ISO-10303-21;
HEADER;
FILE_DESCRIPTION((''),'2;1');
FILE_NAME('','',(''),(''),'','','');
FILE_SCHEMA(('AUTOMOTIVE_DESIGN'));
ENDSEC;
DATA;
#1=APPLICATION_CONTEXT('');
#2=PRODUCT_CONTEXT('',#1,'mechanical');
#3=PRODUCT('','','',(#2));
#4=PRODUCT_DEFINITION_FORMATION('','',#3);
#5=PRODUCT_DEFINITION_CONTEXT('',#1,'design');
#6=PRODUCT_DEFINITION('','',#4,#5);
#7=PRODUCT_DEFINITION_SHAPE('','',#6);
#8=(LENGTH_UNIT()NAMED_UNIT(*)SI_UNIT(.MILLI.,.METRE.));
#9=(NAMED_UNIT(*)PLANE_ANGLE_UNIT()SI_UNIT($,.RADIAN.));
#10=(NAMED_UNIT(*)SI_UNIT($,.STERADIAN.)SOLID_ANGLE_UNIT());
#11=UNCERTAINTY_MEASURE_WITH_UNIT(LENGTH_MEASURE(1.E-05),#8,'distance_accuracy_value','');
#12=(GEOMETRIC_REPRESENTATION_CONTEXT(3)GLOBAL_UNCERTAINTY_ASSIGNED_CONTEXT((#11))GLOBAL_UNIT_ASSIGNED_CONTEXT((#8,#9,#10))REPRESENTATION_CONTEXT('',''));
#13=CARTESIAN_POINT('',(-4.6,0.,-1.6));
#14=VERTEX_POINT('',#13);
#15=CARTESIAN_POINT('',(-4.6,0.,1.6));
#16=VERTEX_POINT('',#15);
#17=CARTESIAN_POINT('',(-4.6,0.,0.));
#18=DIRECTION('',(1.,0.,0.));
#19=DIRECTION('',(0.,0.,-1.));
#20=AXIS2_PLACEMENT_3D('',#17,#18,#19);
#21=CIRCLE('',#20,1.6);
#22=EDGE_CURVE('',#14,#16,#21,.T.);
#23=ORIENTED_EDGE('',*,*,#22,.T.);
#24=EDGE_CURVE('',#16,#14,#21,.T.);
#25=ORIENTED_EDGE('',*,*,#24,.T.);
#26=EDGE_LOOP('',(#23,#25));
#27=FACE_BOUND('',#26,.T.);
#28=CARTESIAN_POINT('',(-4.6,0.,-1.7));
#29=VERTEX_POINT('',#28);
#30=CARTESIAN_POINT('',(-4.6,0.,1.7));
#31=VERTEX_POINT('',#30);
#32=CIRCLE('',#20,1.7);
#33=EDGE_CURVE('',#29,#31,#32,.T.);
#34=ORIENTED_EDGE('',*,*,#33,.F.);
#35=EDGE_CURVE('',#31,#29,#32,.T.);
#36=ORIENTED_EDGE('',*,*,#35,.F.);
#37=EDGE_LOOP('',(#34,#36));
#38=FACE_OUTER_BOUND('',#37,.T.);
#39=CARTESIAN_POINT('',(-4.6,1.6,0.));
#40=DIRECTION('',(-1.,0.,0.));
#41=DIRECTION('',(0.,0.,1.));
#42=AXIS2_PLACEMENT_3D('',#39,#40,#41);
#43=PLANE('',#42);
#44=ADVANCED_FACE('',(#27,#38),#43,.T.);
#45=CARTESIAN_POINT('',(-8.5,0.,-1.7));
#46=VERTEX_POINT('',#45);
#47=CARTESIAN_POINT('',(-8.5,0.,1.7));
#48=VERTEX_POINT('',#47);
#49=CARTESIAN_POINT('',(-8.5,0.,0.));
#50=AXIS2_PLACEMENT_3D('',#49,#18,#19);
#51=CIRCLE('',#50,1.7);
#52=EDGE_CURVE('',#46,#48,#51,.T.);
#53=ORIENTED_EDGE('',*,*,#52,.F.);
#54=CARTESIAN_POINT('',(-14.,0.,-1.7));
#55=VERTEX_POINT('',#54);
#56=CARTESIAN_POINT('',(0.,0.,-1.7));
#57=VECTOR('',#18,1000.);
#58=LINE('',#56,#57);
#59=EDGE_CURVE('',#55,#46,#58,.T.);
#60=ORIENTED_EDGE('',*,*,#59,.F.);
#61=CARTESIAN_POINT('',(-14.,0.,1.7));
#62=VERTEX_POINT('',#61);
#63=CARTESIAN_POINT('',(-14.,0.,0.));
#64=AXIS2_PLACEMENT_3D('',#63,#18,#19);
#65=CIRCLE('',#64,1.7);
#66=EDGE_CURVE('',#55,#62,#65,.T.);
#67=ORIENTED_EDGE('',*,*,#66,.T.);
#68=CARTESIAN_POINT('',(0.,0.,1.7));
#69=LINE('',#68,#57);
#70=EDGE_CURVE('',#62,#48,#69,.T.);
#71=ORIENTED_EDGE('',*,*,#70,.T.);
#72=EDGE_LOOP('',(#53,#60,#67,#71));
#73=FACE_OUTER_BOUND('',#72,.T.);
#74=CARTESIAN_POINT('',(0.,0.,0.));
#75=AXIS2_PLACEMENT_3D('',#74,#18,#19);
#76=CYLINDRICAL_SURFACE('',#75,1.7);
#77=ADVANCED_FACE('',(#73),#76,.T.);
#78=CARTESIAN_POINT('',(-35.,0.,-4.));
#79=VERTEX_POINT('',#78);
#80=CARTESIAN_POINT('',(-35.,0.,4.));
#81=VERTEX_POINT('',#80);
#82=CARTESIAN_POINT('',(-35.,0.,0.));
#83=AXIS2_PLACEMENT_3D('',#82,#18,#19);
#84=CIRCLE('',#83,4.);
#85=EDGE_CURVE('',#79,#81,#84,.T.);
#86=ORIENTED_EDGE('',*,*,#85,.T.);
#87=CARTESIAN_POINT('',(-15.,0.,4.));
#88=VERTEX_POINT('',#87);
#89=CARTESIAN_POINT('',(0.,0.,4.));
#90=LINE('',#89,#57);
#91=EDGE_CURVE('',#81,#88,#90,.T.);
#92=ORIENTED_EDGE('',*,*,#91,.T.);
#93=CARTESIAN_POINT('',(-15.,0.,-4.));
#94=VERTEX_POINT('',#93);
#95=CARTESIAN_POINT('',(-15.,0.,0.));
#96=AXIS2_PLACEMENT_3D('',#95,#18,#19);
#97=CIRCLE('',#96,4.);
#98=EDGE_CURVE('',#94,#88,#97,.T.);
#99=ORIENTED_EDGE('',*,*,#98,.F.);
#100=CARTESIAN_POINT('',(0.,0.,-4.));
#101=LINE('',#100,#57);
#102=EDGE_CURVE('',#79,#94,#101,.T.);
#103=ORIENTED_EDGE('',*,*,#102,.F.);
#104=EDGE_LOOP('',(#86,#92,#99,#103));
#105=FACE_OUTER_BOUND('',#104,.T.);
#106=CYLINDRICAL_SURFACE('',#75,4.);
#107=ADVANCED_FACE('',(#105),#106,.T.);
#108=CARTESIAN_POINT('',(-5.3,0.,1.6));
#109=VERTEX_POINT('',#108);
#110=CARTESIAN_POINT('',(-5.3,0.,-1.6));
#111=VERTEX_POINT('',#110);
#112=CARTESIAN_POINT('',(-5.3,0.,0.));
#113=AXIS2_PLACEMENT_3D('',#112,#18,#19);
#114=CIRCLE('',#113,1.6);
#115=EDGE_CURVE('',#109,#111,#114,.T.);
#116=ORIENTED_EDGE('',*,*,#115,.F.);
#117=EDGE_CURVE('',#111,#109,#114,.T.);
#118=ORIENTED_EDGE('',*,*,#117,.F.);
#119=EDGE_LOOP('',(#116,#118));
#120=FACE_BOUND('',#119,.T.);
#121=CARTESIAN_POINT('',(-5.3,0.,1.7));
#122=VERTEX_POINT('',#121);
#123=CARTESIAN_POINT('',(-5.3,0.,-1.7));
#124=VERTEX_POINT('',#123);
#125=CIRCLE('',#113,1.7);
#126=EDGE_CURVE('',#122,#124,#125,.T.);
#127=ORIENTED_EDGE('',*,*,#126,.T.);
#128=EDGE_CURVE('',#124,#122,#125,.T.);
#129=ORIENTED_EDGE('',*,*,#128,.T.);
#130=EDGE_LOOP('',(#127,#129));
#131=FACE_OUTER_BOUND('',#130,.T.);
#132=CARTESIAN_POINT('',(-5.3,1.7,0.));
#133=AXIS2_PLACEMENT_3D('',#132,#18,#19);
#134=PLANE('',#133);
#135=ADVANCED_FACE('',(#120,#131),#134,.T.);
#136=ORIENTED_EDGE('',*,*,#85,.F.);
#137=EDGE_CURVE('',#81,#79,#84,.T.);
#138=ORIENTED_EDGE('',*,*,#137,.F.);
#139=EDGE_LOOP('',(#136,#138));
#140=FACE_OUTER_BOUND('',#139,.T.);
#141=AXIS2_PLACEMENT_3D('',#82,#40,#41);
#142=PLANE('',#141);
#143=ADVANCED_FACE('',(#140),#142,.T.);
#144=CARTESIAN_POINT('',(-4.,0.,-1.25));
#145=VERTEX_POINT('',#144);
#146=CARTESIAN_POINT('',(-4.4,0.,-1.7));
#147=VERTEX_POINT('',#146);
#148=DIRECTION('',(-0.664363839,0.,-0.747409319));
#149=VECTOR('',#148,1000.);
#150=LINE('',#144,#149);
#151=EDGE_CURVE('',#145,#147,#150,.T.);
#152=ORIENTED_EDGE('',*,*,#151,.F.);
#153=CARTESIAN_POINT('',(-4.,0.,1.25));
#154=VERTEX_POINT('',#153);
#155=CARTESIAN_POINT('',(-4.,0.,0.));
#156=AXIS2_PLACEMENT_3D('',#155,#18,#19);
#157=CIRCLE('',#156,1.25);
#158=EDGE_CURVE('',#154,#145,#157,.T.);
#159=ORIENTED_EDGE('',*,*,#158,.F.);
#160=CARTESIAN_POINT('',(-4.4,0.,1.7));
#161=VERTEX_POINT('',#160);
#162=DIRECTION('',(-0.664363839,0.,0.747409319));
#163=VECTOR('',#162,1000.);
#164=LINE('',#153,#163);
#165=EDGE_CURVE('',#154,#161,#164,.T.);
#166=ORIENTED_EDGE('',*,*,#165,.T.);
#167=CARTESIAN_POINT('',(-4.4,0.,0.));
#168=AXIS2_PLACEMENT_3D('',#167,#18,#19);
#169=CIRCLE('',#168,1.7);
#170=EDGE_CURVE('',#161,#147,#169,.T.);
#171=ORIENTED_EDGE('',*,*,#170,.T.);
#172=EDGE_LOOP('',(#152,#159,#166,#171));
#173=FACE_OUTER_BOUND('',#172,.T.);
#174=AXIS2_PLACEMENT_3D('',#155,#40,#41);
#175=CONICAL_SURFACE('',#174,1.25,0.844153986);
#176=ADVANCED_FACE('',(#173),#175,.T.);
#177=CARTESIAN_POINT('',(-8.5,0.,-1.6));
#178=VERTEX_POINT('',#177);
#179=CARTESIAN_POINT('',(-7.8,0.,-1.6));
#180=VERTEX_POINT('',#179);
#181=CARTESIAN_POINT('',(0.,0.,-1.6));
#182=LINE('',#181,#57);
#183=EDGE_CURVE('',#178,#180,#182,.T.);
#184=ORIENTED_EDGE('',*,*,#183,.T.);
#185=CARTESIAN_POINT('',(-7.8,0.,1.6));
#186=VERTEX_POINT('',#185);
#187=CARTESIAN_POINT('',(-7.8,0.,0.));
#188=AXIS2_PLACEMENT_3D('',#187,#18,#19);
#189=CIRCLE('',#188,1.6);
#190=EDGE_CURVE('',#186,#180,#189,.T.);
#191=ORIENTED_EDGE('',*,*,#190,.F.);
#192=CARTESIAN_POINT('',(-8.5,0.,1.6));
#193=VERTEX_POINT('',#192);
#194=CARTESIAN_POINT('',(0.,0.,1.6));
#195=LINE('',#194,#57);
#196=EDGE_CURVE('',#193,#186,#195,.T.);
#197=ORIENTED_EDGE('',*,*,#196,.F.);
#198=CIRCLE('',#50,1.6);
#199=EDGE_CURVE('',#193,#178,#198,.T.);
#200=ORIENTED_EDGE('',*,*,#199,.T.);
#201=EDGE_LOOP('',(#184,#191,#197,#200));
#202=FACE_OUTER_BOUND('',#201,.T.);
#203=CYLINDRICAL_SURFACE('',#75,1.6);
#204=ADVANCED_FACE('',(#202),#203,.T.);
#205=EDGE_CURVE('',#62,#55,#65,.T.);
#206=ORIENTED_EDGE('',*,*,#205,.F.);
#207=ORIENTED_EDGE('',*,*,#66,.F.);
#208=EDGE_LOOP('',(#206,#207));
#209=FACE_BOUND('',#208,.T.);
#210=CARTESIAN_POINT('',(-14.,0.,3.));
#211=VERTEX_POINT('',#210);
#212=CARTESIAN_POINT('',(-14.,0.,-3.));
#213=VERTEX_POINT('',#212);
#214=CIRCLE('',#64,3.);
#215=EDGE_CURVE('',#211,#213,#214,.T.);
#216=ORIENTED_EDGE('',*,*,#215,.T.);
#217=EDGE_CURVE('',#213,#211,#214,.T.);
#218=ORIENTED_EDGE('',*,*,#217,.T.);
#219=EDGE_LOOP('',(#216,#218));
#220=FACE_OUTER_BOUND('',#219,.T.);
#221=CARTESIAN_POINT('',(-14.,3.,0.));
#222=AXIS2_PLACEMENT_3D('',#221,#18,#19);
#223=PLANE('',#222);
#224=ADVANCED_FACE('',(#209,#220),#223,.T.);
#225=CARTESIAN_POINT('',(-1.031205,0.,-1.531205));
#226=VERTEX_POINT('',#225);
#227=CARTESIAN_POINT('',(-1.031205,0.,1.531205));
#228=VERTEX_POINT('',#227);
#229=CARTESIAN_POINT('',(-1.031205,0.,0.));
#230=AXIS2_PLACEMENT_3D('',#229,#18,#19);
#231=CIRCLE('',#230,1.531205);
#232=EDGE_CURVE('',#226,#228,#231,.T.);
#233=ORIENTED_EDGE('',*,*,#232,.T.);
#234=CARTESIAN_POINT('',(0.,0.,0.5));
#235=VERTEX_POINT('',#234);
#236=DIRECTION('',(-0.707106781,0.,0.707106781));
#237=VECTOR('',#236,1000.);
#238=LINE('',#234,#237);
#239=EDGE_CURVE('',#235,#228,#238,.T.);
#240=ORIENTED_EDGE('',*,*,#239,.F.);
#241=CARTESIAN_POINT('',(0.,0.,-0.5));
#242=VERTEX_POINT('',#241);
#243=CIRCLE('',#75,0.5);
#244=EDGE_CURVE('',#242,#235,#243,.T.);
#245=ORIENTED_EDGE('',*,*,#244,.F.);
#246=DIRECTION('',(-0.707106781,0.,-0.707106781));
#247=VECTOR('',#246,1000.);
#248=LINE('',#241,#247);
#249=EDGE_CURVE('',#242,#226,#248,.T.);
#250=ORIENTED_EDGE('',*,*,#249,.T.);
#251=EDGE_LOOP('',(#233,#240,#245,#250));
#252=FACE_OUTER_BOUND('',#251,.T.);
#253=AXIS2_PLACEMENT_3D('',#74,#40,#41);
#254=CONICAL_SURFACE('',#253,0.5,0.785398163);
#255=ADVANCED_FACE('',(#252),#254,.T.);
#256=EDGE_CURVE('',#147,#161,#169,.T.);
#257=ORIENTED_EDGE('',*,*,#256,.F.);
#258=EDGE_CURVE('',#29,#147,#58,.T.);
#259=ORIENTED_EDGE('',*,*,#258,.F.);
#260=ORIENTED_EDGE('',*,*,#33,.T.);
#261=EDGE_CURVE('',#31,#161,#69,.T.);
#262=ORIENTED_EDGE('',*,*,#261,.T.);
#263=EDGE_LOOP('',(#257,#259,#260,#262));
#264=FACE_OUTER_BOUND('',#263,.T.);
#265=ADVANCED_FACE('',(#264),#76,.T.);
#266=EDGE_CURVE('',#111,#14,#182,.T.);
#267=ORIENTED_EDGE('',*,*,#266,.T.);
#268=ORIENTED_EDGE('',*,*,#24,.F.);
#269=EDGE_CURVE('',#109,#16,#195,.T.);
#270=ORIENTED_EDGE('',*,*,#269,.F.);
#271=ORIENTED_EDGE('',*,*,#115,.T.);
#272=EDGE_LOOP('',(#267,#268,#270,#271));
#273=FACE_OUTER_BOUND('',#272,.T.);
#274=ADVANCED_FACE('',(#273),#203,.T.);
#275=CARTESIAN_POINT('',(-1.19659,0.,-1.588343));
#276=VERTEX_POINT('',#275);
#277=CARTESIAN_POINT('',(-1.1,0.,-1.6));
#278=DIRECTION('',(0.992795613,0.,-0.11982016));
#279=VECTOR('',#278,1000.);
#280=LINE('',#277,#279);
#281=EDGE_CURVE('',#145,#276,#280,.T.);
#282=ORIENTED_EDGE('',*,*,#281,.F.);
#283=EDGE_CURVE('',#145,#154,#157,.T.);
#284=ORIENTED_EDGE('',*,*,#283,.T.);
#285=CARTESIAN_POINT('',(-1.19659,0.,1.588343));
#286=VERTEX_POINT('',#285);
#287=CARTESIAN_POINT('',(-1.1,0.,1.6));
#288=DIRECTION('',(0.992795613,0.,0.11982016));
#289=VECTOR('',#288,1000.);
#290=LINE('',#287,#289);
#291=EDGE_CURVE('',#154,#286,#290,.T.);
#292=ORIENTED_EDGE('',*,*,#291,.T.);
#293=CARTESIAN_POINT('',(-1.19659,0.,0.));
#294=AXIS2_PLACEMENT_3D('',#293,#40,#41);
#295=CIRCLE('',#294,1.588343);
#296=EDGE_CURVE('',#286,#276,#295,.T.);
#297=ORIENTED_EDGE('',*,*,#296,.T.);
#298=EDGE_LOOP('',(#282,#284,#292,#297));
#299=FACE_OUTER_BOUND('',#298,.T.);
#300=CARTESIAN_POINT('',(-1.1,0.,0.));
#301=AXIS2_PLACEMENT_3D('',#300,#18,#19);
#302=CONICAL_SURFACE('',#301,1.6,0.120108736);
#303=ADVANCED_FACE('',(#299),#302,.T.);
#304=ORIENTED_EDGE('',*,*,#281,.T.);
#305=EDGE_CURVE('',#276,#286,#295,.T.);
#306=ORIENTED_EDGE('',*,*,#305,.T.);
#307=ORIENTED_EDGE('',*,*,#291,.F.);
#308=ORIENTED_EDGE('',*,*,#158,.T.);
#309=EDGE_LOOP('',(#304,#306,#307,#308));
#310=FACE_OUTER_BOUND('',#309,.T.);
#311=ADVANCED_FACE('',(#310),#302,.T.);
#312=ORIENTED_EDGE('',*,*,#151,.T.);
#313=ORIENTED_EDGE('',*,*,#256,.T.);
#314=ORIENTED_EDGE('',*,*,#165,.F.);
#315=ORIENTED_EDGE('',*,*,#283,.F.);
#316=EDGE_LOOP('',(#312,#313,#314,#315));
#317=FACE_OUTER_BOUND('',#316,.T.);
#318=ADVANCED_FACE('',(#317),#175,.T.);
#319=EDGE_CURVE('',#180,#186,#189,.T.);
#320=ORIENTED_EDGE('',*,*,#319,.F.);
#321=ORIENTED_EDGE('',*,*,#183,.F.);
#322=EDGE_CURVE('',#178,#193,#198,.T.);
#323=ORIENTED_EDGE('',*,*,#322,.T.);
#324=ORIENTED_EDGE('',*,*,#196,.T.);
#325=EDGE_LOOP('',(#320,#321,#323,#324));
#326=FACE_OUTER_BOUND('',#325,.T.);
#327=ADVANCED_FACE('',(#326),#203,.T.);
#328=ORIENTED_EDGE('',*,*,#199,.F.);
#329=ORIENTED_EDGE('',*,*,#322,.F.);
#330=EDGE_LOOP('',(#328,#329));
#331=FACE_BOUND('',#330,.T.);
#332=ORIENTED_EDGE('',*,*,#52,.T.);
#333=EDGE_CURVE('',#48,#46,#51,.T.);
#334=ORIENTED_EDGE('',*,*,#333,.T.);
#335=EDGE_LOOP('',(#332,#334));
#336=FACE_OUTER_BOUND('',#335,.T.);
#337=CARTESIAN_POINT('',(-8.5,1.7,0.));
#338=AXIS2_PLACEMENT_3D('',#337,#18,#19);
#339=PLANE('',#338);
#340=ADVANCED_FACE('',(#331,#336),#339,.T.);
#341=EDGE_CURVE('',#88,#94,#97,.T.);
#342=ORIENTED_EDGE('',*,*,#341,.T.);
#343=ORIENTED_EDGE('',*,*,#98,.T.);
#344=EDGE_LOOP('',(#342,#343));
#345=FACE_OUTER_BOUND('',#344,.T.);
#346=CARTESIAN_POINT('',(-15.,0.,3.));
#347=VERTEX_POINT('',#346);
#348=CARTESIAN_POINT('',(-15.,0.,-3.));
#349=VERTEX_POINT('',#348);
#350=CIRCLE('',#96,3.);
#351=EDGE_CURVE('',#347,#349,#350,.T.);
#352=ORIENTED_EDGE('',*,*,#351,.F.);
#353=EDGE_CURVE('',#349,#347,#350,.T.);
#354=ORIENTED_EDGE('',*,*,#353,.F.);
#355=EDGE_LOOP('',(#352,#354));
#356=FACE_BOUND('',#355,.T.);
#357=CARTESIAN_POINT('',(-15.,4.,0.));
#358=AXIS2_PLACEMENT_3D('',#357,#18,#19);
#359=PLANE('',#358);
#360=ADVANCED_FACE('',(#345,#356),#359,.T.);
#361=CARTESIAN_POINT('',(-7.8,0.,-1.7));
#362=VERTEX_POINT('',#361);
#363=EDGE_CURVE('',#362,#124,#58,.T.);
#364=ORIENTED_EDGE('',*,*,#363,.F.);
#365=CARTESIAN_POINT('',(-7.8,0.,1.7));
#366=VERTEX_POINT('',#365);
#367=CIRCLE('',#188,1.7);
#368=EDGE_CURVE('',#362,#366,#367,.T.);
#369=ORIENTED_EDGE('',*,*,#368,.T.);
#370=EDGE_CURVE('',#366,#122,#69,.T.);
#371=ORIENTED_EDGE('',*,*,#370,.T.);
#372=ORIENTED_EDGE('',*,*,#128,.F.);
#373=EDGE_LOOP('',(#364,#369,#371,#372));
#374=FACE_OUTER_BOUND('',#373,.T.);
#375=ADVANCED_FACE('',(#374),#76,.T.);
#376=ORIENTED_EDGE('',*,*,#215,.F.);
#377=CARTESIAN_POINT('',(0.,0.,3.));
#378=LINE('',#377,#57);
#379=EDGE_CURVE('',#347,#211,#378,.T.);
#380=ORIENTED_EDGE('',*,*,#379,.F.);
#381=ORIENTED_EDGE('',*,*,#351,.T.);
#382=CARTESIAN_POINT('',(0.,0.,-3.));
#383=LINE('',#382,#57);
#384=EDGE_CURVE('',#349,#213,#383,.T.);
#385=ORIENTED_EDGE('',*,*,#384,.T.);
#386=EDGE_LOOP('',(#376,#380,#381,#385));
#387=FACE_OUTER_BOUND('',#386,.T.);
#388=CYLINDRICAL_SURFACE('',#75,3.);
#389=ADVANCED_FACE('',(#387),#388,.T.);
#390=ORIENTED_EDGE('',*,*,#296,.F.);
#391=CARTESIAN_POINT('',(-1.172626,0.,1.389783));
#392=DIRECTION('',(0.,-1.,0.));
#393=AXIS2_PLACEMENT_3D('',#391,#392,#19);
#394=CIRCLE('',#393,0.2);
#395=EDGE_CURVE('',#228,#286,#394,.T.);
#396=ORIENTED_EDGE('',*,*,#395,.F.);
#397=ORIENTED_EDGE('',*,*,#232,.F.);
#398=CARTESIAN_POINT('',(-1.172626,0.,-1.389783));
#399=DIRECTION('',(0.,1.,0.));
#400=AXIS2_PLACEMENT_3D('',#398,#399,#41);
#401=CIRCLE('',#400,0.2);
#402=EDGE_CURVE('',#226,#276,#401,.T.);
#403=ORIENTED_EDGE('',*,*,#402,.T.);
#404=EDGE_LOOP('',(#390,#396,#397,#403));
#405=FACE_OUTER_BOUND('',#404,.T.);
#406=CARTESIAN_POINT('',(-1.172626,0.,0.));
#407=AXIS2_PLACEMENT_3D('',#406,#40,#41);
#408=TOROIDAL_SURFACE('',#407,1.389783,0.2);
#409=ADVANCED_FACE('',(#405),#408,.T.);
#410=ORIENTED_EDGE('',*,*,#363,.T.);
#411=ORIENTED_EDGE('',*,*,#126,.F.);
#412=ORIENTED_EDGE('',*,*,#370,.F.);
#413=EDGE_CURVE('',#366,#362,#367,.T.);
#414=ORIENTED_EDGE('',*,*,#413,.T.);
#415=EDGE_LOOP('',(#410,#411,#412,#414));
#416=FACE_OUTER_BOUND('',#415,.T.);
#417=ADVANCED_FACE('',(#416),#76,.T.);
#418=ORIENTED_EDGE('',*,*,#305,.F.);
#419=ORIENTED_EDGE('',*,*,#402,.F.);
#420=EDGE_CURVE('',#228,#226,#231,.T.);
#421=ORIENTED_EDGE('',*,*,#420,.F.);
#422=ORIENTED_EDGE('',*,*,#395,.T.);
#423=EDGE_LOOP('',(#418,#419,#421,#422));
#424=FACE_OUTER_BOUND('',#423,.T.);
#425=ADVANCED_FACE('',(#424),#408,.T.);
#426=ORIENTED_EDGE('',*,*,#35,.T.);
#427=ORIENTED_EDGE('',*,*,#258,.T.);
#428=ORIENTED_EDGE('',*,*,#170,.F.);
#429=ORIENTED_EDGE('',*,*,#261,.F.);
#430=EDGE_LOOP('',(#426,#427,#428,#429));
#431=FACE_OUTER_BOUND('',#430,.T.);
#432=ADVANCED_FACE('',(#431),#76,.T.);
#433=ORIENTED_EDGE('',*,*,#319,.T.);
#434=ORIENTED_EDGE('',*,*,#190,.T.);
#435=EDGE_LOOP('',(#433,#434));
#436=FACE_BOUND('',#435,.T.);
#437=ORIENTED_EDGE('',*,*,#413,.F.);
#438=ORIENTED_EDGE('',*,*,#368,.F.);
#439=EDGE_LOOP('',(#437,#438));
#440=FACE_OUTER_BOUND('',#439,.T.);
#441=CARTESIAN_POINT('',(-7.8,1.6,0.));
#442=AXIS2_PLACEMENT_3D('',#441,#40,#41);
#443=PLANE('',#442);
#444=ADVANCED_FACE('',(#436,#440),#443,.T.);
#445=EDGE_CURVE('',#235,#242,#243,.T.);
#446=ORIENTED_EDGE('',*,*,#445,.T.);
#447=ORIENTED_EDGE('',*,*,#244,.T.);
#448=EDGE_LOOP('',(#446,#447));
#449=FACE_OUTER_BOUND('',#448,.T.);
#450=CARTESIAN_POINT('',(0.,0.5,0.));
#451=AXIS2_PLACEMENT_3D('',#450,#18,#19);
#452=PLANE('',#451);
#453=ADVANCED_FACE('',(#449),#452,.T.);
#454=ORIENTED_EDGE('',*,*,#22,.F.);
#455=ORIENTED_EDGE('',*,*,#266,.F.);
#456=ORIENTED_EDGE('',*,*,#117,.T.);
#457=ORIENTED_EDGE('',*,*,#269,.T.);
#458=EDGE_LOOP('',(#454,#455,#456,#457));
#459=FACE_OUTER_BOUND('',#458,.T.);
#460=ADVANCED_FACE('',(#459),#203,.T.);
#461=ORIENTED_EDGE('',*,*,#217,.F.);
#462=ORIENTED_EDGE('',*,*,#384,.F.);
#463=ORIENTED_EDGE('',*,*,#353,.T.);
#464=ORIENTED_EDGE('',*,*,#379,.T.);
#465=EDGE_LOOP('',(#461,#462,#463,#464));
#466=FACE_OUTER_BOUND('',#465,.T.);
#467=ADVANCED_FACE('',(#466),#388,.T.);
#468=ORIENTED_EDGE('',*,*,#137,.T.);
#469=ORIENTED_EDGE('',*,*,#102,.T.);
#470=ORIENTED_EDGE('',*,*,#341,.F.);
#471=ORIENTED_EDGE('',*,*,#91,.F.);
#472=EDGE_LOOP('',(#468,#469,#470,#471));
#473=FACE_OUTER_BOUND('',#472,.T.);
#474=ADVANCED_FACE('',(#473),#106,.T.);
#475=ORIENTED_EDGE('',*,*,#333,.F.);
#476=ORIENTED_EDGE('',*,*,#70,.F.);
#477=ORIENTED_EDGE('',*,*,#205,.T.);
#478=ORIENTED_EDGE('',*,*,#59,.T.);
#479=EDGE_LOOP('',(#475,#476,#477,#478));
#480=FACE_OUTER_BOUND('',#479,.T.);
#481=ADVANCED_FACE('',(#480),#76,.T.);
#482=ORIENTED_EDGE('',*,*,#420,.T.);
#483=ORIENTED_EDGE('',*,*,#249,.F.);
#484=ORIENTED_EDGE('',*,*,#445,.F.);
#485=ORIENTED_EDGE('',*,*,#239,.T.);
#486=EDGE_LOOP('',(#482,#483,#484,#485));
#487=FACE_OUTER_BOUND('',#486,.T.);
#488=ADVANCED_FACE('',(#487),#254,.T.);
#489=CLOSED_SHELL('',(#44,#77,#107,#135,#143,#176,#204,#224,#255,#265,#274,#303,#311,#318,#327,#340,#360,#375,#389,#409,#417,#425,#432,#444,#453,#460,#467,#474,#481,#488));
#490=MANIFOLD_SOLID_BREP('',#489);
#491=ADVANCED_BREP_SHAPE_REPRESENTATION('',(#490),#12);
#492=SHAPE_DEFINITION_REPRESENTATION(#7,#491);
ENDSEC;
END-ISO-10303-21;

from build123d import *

# Parameters (mm, degrees)
EDGE_FILLET_R0_2_R = 0.2


with BuildPart() as part:
    # Plug Profile Sketch → Plug Body Revolve (revolve)
    with BuildSketch(Plane.XY, mode=Mode.PRIVATE) as plug_body_revolve_sk:
        Polygon((0, 0), (-35, 0), (-35, 4), (-15, 4), (-15, 3), (-14, 3), (-14, 1.7), (-8.5, 1.7), (-8.5, 1.6), (-7.8, 1.6), (-7.8, 1.7), (-5.3, 1.7), (-5.3, 1.6), (-4.6, 1.6), (-4.6, 1.7), (-4.4, 1.7), (-4, 1.25), (-1.1, 1.6), (0, 0.5), align=None)
    revolve(plug_body_revolve_sk.sketch.rotate(Axis((0, 0, 0), (-1, 0, 0)), 90), axis=Axis((0, 0, 0), (-1, 0, 0)))

    # Edge Fillet R0.2
    edge_fillet_r0_2_edges = [part.edges().sort_by_distance(p)[0] for p in [
        (-1.1, 0, 1.6),
    ]]
    fillet(edge_fillet_r0_2_edges, radius=EDGE_FILLET_R0_2_R)


solid = part.part
